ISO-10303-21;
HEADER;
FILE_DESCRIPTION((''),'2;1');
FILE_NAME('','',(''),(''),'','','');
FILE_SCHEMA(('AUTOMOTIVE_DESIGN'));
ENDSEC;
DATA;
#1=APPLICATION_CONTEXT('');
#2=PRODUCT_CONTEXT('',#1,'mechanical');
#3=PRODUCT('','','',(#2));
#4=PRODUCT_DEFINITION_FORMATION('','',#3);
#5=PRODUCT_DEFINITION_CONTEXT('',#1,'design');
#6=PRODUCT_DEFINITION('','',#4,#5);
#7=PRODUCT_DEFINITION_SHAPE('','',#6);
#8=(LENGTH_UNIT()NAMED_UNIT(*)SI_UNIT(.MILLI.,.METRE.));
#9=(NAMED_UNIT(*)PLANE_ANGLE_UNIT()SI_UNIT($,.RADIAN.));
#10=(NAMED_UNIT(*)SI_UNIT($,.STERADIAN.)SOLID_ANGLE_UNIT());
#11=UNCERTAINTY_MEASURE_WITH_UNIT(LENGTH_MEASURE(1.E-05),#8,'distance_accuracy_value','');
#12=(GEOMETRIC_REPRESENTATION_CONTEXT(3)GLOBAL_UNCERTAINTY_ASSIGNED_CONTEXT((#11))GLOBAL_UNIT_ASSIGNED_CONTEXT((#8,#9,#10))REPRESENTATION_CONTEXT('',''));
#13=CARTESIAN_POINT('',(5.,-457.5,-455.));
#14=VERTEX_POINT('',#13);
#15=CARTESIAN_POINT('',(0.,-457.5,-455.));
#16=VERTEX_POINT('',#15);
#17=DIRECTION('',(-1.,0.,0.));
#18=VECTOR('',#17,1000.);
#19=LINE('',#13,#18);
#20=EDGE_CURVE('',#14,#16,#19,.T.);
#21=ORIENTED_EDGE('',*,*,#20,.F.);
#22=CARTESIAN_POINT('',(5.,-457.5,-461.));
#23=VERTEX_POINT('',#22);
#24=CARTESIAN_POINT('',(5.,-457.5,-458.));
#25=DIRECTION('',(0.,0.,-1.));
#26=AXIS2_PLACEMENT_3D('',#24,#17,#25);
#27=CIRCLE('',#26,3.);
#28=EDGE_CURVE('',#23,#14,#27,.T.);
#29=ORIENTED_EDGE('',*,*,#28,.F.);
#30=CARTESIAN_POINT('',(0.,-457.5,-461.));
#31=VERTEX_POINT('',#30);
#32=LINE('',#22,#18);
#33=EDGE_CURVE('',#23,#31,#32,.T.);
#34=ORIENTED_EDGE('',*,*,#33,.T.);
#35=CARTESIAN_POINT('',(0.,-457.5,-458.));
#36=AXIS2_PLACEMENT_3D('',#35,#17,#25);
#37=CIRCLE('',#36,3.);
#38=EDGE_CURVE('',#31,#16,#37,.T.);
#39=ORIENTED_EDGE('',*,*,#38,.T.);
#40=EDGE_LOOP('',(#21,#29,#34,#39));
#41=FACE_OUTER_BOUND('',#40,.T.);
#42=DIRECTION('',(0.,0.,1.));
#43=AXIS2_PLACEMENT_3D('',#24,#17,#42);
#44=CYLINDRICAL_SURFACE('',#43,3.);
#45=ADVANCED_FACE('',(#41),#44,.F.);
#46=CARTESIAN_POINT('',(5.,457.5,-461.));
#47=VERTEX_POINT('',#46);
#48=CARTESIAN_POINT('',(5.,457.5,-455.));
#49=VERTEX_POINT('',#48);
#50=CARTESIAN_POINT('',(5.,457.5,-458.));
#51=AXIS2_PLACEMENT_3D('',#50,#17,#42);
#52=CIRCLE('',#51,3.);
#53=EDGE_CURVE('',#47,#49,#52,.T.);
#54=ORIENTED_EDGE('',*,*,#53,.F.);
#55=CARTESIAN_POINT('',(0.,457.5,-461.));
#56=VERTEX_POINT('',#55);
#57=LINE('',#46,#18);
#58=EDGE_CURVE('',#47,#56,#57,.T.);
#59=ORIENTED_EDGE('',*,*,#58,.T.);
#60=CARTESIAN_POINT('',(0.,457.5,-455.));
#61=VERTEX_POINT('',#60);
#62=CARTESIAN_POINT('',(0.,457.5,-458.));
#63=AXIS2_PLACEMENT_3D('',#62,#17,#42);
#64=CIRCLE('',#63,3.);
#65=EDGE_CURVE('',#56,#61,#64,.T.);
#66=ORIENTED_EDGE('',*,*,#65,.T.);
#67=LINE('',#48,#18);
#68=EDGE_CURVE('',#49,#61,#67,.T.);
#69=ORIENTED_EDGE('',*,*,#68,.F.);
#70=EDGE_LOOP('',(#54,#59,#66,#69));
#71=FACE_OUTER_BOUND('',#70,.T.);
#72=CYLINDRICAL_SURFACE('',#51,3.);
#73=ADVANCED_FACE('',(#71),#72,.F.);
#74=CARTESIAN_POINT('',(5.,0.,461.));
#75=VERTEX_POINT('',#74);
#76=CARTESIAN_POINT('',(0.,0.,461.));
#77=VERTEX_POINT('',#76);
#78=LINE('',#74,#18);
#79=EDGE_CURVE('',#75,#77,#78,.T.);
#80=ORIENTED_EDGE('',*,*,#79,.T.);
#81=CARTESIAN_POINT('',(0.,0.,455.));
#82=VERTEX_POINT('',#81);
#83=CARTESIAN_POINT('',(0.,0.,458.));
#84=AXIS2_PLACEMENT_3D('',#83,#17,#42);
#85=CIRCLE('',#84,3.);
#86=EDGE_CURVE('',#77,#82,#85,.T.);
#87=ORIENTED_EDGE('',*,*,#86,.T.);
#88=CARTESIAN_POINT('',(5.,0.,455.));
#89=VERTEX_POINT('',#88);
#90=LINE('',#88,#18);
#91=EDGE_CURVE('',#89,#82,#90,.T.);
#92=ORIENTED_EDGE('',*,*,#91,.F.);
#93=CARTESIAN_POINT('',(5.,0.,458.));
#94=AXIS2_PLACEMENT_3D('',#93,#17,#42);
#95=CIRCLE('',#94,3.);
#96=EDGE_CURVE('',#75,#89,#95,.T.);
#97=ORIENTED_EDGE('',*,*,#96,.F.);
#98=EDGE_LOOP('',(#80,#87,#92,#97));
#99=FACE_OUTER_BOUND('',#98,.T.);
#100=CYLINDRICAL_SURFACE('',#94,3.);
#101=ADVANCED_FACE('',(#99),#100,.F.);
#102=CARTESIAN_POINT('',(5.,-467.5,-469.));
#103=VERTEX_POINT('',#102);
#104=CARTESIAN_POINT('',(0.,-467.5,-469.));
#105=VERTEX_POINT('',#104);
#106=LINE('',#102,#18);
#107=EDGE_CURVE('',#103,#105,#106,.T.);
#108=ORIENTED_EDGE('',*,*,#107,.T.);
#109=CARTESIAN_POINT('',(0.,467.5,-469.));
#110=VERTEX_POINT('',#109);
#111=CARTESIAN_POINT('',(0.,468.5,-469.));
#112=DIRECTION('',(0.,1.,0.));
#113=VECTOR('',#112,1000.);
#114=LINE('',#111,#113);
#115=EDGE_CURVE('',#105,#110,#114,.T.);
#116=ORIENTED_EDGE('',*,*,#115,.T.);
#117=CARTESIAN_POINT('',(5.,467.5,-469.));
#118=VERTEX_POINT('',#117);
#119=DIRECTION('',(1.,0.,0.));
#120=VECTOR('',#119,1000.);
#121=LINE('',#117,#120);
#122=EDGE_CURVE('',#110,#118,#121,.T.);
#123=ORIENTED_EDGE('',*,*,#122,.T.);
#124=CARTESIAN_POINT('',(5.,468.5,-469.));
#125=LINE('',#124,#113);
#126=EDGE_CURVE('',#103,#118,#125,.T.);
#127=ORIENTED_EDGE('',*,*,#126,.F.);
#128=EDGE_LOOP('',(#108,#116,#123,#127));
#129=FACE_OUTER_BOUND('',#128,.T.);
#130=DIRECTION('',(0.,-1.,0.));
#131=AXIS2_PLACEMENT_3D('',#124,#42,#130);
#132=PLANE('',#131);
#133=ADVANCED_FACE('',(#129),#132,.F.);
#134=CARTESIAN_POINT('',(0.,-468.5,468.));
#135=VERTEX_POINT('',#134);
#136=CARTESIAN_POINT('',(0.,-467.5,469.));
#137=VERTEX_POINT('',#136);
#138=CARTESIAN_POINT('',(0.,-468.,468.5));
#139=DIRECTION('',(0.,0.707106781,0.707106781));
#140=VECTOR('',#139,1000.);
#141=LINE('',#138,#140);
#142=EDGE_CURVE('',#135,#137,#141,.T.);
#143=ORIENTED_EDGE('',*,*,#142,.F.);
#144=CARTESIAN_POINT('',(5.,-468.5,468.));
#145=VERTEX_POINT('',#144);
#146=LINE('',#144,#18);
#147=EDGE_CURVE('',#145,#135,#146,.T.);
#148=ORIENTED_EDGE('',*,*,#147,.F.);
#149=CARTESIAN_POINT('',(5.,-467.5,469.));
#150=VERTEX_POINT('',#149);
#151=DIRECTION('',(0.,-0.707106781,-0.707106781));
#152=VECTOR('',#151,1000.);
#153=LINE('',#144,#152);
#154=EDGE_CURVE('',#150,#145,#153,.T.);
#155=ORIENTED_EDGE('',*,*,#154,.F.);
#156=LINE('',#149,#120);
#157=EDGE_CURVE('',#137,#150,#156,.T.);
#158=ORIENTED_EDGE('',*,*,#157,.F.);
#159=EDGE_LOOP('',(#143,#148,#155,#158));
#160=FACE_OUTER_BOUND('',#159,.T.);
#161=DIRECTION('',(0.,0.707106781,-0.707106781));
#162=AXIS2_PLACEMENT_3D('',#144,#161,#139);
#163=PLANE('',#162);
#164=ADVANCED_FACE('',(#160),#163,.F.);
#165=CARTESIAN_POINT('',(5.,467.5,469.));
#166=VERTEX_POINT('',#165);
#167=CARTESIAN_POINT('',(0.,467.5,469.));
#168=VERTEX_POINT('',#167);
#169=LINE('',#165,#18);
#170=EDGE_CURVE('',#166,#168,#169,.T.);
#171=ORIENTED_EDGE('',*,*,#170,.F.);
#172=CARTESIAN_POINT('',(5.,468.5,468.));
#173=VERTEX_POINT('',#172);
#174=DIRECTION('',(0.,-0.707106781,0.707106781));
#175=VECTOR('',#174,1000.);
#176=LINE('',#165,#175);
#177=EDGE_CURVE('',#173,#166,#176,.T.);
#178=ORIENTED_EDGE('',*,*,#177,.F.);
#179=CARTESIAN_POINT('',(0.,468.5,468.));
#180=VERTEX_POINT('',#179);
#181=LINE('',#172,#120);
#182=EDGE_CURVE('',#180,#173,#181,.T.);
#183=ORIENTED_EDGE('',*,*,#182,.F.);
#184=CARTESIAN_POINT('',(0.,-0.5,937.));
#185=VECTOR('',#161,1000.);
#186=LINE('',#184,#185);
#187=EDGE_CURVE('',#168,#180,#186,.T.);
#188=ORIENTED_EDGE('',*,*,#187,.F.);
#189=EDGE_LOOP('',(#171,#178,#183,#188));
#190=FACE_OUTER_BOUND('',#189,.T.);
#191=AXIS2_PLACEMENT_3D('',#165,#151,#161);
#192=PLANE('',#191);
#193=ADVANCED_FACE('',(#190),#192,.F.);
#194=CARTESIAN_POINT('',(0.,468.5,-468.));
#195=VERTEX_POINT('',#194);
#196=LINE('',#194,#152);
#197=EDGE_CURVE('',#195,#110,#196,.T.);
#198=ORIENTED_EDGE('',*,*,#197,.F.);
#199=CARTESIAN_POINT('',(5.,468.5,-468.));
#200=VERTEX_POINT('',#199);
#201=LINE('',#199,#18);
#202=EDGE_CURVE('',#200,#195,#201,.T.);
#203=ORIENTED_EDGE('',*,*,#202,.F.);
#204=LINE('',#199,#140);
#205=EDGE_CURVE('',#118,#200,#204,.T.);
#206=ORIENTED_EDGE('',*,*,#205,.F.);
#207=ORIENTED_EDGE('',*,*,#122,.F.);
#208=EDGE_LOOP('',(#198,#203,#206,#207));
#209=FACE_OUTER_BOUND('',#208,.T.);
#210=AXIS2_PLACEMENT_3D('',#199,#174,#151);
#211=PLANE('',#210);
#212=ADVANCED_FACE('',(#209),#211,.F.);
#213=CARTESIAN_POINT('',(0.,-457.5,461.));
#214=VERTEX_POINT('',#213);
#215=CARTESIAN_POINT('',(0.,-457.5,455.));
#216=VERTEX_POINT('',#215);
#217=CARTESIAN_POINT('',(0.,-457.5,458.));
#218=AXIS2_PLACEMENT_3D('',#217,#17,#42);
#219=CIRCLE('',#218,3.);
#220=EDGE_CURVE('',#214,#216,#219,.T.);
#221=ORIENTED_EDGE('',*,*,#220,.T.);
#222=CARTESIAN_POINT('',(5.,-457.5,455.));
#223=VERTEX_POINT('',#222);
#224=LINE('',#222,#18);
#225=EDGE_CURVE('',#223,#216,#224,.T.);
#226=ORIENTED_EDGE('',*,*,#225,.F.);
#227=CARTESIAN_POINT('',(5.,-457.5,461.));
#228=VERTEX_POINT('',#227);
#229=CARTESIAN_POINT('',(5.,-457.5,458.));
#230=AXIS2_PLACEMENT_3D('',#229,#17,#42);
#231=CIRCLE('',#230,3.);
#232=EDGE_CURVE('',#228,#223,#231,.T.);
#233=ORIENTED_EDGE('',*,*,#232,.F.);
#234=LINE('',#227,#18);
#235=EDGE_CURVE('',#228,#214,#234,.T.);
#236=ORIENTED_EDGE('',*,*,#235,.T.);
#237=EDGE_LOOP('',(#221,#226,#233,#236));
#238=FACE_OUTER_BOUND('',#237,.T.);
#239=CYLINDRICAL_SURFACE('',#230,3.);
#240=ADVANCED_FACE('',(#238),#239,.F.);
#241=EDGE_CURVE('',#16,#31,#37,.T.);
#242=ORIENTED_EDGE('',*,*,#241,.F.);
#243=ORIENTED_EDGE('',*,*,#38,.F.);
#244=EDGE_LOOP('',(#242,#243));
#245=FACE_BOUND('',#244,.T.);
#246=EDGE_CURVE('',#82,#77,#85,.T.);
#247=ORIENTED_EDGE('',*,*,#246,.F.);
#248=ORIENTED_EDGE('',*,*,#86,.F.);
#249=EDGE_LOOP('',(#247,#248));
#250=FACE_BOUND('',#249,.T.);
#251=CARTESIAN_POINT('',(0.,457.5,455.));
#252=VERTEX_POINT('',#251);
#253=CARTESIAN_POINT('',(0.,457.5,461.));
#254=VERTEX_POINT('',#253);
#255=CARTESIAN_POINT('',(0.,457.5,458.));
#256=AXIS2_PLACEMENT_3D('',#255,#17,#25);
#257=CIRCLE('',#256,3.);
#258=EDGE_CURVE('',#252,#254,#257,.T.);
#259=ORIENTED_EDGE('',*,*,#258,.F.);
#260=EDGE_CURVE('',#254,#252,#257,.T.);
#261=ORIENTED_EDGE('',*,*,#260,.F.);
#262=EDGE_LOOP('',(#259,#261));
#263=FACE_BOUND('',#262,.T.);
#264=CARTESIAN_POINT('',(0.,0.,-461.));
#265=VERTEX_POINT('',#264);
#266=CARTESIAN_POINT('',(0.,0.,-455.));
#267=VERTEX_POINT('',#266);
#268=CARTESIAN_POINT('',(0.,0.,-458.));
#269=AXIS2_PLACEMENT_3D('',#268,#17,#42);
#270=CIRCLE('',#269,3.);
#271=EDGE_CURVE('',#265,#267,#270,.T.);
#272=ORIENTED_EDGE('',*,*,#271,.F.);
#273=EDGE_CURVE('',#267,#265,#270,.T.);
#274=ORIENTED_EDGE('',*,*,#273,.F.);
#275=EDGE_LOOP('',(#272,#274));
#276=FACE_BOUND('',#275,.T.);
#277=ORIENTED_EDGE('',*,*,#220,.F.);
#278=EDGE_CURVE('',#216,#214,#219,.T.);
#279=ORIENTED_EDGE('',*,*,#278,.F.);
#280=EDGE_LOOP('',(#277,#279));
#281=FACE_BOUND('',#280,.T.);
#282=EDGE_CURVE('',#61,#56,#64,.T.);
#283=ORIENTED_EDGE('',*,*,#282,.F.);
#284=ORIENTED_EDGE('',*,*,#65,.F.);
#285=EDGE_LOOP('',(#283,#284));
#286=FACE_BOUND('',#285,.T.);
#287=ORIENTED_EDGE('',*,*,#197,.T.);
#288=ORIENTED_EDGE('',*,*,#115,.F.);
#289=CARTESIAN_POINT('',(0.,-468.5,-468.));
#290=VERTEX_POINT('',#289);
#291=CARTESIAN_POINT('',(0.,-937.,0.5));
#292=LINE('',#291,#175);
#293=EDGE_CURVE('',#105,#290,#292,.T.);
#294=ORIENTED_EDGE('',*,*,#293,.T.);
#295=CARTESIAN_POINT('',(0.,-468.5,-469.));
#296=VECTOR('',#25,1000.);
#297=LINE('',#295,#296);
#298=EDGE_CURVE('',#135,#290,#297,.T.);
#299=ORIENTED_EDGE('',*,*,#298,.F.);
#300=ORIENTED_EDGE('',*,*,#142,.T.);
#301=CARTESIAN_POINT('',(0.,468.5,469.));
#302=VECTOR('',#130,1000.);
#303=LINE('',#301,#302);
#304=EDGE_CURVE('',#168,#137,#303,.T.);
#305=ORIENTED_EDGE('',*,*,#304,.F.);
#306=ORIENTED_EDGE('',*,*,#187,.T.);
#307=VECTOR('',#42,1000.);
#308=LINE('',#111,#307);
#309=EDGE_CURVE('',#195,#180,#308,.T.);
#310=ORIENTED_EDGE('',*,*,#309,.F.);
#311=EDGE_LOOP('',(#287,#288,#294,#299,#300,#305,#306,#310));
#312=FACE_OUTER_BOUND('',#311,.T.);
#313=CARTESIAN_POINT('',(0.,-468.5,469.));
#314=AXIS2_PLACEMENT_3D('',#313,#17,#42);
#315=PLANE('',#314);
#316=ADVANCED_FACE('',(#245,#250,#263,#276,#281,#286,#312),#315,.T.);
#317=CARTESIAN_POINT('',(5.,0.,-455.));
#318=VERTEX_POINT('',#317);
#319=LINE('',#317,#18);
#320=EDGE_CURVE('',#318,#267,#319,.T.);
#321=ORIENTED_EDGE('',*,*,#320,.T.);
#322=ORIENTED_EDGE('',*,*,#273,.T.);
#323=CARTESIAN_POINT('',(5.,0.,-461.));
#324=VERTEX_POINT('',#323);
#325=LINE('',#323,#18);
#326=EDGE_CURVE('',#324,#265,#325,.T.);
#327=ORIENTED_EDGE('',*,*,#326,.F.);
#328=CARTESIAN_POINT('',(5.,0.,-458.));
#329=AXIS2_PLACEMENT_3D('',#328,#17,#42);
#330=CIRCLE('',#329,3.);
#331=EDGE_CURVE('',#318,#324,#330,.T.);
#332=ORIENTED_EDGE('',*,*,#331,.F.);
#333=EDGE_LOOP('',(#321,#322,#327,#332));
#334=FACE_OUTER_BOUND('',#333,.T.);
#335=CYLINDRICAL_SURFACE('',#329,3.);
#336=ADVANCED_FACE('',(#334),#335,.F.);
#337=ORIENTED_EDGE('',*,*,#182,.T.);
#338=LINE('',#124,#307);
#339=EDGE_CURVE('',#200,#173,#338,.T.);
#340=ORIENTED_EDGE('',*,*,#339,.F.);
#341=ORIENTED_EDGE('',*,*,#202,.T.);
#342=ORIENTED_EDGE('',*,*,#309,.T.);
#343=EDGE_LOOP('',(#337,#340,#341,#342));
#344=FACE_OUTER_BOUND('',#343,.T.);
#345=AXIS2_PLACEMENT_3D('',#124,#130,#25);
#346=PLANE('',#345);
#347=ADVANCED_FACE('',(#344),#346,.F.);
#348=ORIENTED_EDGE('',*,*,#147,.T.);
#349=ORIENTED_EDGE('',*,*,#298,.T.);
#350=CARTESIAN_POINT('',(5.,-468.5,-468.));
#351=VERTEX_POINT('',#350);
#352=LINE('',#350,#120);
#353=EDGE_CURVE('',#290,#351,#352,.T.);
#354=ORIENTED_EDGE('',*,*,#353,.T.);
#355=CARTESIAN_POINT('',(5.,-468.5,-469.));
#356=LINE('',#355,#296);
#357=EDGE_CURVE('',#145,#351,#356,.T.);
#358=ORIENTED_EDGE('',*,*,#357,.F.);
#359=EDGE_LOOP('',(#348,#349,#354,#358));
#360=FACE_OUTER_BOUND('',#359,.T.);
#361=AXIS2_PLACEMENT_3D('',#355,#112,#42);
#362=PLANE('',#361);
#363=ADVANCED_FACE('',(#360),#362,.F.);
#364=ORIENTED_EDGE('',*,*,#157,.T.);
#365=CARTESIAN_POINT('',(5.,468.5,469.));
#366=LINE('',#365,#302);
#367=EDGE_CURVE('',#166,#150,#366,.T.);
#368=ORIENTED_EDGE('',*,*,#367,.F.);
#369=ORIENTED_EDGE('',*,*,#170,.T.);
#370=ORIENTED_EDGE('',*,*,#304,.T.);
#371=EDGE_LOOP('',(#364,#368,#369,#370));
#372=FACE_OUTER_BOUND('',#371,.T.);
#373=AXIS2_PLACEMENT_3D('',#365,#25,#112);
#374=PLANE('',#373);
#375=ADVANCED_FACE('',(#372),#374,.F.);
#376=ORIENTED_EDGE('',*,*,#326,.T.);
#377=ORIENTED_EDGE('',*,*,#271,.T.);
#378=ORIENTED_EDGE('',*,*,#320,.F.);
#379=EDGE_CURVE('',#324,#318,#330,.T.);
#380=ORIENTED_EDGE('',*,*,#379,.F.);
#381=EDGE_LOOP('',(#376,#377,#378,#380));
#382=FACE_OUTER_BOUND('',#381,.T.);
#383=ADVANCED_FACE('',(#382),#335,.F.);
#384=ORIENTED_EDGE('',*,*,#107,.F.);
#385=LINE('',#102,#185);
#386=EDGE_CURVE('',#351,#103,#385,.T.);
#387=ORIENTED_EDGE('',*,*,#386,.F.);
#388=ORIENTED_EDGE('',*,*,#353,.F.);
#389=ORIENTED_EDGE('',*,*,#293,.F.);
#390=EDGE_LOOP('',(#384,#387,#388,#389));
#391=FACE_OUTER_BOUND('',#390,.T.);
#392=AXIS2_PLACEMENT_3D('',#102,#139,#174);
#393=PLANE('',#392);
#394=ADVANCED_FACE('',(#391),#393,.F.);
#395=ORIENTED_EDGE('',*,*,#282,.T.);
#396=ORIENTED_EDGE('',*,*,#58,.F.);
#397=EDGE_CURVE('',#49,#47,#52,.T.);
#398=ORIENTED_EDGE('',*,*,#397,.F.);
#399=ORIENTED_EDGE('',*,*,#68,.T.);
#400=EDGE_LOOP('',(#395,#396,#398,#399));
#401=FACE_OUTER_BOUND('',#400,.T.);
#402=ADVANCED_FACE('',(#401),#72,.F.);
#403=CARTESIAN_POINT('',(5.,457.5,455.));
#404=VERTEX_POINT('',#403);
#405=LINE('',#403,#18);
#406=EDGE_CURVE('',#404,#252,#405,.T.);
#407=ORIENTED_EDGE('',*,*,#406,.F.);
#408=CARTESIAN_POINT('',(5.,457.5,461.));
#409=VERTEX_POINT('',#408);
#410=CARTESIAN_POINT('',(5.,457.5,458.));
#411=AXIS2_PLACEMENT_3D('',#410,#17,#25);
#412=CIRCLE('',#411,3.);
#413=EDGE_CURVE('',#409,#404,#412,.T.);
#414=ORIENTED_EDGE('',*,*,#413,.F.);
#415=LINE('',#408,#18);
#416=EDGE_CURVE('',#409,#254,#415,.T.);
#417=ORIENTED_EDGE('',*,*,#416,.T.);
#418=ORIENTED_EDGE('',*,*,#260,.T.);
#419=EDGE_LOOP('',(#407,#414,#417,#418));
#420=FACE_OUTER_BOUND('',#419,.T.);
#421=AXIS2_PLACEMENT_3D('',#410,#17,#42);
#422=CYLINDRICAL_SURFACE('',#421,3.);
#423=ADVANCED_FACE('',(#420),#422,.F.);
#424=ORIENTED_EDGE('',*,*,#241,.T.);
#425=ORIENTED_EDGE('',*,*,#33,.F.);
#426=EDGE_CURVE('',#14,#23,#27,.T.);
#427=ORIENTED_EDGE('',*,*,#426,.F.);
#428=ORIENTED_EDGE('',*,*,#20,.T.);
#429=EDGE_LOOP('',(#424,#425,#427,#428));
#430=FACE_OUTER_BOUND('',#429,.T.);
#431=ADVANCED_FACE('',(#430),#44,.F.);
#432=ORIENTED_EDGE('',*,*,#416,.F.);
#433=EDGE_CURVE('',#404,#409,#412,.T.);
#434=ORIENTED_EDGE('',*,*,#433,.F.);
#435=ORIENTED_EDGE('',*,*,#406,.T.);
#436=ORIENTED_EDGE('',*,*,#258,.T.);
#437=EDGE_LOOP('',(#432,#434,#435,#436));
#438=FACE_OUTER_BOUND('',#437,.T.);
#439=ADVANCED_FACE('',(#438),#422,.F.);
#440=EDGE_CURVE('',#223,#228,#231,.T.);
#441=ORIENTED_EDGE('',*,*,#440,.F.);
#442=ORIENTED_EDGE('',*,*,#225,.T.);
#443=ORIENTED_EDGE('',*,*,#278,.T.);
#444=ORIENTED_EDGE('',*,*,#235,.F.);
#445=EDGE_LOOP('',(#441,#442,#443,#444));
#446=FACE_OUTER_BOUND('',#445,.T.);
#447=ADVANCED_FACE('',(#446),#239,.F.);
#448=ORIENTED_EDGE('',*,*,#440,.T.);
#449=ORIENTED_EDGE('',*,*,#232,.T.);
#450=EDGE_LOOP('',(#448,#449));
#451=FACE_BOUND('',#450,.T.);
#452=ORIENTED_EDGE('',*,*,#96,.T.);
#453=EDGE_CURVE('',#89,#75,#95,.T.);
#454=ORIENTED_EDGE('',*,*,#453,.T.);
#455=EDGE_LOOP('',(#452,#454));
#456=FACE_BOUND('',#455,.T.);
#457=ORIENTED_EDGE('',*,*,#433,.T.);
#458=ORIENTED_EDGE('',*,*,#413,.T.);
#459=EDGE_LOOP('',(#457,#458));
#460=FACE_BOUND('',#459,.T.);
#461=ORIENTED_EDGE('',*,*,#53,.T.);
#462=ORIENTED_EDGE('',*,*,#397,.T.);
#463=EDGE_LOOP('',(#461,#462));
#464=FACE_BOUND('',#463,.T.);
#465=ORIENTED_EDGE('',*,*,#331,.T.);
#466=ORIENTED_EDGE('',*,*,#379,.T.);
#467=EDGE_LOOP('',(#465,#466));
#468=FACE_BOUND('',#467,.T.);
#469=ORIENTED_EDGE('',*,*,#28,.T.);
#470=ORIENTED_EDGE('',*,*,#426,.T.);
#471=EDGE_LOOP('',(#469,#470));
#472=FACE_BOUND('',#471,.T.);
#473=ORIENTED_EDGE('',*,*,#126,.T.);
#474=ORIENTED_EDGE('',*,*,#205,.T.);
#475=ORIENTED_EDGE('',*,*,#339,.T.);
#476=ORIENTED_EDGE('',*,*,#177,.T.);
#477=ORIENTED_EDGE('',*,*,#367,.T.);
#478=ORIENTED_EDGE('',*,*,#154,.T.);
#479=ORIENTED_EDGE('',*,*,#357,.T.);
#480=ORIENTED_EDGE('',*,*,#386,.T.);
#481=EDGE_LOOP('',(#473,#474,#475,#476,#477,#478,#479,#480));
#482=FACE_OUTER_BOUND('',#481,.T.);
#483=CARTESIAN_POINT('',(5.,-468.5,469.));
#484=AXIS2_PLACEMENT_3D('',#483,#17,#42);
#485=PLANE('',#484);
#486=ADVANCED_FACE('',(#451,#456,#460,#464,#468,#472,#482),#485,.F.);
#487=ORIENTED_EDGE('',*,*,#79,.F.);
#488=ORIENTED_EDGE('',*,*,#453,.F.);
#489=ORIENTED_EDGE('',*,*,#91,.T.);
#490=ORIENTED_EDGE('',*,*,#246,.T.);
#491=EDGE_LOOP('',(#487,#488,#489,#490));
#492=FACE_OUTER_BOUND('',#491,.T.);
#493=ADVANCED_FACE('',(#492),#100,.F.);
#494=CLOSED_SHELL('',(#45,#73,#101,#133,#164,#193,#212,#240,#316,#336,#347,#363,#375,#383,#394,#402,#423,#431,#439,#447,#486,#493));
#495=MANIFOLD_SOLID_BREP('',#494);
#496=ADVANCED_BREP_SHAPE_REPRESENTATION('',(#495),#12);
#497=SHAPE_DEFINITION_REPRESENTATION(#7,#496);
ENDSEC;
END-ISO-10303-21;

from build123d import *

# Parameters (mm, degrees)
SKETCH_1_W          = 938
SKETCH_1_H          = 937
EXTRUDE_1_DEPTH     = 5
CHAMFER_1_SIZE      = 1
SKETCH_2_R          = 3
CUT_EXTRUDE_1_DEPTH = 663.931557553


with BuildPart() as part:
    # 草图1 → 凸台-拉伸1 (new body)
    with BuildSketch(Plane(origin=(0, 0, 0), x_dir=(0, 0, -1), z_dir=(1, 0, 0))):
        Rectangle(SKETCH_1_W, SKETCH_1_H)
    extrude(amount=EXTRUDE_1_DEPTH)

    # 倒角1
    chamfer_1_edges = [part.edges().sort_by_distance(p)[0] for p in [
        (2.5, 468.5, 469),
        (2.5, 468.5, -469),
        (2.5, -468.5, -469),
        (2.5, -468.5, 469),
    ]]
    chamfer(chamfer_1_edges, length=CHAMFER_1_SIZE)

    # 草图2 → 切除-拉伸1 (cut, through all)
    with BuildSketch(Plane.ZY):
        with Locations((-458, 457.5)):
            Circle(SKETCH_2_R)
        with Locations(Location((-458, -457.5, 0), (0, 0, 180))):
            Circle(SKETCH_2_R)
        with Locations((458, -457.5)):
            Circle(SKETCH_2_R)
        with Locations(Location((458, 457.5, 0), (0, 0, 180))):
            Circle(SKETCH_2_R)
        with Locations((458, 0)):
            Circle(SKETCH_2_R)
        with Locations((-458, 0)):
            Circle(SKETCH_2_R)
    extrude(amount=-CUT_EXTRUDE_1_DEPTH, mode=Mode.SUBTRACT)


solid = part.part
